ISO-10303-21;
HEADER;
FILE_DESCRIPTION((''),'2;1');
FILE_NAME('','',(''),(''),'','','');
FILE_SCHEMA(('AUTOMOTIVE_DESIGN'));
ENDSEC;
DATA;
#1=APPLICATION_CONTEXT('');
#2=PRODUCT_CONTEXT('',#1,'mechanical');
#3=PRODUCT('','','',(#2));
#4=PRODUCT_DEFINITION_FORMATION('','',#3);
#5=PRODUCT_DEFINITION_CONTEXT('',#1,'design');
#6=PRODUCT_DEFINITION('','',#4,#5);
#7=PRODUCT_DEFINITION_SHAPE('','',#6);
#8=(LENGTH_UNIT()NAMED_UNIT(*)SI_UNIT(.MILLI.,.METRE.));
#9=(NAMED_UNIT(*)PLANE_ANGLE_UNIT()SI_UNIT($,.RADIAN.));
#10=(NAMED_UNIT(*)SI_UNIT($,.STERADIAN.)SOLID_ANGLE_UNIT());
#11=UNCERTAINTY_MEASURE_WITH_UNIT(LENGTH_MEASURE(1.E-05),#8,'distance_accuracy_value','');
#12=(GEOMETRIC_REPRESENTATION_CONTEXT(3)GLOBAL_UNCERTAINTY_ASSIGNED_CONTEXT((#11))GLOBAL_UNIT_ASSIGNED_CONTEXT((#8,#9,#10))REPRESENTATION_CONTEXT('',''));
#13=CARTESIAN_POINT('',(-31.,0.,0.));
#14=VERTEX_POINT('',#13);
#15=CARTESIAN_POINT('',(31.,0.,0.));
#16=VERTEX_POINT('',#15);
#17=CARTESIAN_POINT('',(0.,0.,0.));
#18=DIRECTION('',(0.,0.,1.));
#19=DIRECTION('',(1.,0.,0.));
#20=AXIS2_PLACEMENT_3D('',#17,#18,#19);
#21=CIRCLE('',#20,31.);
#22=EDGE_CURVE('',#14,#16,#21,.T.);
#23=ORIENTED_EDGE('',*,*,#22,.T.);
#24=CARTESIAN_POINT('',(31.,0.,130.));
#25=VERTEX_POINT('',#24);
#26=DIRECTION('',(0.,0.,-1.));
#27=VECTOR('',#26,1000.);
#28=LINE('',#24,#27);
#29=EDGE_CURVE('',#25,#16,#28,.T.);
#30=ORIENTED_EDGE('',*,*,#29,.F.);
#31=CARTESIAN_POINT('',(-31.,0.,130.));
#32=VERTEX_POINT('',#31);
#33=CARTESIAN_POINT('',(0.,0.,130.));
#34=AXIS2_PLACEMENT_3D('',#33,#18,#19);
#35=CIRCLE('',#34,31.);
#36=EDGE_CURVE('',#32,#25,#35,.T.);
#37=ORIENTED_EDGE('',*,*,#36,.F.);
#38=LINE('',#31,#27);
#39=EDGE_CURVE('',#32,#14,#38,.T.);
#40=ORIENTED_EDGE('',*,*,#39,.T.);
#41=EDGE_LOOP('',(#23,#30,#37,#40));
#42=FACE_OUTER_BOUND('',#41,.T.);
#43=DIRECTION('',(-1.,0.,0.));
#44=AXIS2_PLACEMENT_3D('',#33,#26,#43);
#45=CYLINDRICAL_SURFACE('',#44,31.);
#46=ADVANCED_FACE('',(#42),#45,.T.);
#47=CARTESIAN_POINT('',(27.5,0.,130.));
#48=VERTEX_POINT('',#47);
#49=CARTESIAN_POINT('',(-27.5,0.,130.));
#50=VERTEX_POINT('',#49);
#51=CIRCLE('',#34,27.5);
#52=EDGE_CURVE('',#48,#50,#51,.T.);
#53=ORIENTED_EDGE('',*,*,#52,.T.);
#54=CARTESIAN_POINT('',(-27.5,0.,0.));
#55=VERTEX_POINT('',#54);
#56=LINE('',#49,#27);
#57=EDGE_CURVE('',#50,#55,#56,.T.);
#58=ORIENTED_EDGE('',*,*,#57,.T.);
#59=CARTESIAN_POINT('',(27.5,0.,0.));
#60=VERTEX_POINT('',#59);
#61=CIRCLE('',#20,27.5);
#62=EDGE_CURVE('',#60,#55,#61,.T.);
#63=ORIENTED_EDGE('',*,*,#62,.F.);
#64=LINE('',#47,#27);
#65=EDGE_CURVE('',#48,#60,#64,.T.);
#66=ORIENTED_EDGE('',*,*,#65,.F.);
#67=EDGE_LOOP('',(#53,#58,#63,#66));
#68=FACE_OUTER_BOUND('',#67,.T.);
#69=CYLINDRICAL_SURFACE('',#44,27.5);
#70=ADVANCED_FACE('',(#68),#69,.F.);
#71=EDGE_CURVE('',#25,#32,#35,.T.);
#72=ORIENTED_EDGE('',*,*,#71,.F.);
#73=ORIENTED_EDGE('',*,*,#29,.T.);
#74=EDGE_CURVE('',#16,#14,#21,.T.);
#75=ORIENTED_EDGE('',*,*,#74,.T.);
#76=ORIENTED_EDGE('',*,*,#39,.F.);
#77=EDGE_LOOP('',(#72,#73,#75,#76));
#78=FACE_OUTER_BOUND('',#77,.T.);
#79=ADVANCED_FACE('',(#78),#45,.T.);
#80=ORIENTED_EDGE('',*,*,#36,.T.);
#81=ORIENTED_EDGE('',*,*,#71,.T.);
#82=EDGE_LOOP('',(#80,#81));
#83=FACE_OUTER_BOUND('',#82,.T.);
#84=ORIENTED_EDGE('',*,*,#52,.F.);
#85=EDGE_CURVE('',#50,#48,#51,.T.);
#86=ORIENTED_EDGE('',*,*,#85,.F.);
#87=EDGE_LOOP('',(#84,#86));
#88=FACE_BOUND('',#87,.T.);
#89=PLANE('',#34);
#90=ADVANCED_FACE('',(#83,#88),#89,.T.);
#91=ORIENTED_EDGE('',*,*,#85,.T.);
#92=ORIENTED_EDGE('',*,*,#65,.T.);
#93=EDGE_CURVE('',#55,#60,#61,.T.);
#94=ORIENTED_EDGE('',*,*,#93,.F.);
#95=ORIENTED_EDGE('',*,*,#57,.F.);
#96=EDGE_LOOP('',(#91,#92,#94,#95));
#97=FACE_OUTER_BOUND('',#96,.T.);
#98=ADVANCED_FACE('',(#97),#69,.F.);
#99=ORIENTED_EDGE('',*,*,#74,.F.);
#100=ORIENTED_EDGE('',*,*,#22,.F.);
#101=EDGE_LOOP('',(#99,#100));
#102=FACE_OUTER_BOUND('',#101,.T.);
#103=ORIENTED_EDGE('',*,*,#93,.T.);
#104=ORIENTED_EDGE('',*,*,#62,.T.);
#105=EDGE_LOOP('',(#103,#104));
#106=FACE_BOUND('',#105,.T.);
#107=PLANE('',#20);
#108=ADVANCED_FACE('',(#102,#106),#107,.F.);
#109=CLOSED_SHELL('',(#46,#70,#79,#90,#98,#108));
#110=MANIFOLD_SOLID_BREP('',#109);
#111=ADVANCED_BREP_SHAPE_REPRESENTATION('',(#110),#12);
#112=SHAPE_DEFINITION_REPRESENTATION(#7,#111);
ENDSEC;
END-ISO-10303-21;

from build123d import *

# Parameters (mm, degrees)
SKETCH_1_R      = 31
SKETCH_1_R_2    = 27.5
EXTRUDE_1_DEPTH = 130


with BuildPart() as part:
    # 草图1 → 凸台-拉伸1 (new body)
    with BuildSketch(Plane.XY):
        Circle(SKETCH_1_R)
        Circle(SKETCH_1_R_2, mode=Mode.SUBTRACT)
    extrude(amount=EXTRUDE_1_DEPTH)


solid = part.part
